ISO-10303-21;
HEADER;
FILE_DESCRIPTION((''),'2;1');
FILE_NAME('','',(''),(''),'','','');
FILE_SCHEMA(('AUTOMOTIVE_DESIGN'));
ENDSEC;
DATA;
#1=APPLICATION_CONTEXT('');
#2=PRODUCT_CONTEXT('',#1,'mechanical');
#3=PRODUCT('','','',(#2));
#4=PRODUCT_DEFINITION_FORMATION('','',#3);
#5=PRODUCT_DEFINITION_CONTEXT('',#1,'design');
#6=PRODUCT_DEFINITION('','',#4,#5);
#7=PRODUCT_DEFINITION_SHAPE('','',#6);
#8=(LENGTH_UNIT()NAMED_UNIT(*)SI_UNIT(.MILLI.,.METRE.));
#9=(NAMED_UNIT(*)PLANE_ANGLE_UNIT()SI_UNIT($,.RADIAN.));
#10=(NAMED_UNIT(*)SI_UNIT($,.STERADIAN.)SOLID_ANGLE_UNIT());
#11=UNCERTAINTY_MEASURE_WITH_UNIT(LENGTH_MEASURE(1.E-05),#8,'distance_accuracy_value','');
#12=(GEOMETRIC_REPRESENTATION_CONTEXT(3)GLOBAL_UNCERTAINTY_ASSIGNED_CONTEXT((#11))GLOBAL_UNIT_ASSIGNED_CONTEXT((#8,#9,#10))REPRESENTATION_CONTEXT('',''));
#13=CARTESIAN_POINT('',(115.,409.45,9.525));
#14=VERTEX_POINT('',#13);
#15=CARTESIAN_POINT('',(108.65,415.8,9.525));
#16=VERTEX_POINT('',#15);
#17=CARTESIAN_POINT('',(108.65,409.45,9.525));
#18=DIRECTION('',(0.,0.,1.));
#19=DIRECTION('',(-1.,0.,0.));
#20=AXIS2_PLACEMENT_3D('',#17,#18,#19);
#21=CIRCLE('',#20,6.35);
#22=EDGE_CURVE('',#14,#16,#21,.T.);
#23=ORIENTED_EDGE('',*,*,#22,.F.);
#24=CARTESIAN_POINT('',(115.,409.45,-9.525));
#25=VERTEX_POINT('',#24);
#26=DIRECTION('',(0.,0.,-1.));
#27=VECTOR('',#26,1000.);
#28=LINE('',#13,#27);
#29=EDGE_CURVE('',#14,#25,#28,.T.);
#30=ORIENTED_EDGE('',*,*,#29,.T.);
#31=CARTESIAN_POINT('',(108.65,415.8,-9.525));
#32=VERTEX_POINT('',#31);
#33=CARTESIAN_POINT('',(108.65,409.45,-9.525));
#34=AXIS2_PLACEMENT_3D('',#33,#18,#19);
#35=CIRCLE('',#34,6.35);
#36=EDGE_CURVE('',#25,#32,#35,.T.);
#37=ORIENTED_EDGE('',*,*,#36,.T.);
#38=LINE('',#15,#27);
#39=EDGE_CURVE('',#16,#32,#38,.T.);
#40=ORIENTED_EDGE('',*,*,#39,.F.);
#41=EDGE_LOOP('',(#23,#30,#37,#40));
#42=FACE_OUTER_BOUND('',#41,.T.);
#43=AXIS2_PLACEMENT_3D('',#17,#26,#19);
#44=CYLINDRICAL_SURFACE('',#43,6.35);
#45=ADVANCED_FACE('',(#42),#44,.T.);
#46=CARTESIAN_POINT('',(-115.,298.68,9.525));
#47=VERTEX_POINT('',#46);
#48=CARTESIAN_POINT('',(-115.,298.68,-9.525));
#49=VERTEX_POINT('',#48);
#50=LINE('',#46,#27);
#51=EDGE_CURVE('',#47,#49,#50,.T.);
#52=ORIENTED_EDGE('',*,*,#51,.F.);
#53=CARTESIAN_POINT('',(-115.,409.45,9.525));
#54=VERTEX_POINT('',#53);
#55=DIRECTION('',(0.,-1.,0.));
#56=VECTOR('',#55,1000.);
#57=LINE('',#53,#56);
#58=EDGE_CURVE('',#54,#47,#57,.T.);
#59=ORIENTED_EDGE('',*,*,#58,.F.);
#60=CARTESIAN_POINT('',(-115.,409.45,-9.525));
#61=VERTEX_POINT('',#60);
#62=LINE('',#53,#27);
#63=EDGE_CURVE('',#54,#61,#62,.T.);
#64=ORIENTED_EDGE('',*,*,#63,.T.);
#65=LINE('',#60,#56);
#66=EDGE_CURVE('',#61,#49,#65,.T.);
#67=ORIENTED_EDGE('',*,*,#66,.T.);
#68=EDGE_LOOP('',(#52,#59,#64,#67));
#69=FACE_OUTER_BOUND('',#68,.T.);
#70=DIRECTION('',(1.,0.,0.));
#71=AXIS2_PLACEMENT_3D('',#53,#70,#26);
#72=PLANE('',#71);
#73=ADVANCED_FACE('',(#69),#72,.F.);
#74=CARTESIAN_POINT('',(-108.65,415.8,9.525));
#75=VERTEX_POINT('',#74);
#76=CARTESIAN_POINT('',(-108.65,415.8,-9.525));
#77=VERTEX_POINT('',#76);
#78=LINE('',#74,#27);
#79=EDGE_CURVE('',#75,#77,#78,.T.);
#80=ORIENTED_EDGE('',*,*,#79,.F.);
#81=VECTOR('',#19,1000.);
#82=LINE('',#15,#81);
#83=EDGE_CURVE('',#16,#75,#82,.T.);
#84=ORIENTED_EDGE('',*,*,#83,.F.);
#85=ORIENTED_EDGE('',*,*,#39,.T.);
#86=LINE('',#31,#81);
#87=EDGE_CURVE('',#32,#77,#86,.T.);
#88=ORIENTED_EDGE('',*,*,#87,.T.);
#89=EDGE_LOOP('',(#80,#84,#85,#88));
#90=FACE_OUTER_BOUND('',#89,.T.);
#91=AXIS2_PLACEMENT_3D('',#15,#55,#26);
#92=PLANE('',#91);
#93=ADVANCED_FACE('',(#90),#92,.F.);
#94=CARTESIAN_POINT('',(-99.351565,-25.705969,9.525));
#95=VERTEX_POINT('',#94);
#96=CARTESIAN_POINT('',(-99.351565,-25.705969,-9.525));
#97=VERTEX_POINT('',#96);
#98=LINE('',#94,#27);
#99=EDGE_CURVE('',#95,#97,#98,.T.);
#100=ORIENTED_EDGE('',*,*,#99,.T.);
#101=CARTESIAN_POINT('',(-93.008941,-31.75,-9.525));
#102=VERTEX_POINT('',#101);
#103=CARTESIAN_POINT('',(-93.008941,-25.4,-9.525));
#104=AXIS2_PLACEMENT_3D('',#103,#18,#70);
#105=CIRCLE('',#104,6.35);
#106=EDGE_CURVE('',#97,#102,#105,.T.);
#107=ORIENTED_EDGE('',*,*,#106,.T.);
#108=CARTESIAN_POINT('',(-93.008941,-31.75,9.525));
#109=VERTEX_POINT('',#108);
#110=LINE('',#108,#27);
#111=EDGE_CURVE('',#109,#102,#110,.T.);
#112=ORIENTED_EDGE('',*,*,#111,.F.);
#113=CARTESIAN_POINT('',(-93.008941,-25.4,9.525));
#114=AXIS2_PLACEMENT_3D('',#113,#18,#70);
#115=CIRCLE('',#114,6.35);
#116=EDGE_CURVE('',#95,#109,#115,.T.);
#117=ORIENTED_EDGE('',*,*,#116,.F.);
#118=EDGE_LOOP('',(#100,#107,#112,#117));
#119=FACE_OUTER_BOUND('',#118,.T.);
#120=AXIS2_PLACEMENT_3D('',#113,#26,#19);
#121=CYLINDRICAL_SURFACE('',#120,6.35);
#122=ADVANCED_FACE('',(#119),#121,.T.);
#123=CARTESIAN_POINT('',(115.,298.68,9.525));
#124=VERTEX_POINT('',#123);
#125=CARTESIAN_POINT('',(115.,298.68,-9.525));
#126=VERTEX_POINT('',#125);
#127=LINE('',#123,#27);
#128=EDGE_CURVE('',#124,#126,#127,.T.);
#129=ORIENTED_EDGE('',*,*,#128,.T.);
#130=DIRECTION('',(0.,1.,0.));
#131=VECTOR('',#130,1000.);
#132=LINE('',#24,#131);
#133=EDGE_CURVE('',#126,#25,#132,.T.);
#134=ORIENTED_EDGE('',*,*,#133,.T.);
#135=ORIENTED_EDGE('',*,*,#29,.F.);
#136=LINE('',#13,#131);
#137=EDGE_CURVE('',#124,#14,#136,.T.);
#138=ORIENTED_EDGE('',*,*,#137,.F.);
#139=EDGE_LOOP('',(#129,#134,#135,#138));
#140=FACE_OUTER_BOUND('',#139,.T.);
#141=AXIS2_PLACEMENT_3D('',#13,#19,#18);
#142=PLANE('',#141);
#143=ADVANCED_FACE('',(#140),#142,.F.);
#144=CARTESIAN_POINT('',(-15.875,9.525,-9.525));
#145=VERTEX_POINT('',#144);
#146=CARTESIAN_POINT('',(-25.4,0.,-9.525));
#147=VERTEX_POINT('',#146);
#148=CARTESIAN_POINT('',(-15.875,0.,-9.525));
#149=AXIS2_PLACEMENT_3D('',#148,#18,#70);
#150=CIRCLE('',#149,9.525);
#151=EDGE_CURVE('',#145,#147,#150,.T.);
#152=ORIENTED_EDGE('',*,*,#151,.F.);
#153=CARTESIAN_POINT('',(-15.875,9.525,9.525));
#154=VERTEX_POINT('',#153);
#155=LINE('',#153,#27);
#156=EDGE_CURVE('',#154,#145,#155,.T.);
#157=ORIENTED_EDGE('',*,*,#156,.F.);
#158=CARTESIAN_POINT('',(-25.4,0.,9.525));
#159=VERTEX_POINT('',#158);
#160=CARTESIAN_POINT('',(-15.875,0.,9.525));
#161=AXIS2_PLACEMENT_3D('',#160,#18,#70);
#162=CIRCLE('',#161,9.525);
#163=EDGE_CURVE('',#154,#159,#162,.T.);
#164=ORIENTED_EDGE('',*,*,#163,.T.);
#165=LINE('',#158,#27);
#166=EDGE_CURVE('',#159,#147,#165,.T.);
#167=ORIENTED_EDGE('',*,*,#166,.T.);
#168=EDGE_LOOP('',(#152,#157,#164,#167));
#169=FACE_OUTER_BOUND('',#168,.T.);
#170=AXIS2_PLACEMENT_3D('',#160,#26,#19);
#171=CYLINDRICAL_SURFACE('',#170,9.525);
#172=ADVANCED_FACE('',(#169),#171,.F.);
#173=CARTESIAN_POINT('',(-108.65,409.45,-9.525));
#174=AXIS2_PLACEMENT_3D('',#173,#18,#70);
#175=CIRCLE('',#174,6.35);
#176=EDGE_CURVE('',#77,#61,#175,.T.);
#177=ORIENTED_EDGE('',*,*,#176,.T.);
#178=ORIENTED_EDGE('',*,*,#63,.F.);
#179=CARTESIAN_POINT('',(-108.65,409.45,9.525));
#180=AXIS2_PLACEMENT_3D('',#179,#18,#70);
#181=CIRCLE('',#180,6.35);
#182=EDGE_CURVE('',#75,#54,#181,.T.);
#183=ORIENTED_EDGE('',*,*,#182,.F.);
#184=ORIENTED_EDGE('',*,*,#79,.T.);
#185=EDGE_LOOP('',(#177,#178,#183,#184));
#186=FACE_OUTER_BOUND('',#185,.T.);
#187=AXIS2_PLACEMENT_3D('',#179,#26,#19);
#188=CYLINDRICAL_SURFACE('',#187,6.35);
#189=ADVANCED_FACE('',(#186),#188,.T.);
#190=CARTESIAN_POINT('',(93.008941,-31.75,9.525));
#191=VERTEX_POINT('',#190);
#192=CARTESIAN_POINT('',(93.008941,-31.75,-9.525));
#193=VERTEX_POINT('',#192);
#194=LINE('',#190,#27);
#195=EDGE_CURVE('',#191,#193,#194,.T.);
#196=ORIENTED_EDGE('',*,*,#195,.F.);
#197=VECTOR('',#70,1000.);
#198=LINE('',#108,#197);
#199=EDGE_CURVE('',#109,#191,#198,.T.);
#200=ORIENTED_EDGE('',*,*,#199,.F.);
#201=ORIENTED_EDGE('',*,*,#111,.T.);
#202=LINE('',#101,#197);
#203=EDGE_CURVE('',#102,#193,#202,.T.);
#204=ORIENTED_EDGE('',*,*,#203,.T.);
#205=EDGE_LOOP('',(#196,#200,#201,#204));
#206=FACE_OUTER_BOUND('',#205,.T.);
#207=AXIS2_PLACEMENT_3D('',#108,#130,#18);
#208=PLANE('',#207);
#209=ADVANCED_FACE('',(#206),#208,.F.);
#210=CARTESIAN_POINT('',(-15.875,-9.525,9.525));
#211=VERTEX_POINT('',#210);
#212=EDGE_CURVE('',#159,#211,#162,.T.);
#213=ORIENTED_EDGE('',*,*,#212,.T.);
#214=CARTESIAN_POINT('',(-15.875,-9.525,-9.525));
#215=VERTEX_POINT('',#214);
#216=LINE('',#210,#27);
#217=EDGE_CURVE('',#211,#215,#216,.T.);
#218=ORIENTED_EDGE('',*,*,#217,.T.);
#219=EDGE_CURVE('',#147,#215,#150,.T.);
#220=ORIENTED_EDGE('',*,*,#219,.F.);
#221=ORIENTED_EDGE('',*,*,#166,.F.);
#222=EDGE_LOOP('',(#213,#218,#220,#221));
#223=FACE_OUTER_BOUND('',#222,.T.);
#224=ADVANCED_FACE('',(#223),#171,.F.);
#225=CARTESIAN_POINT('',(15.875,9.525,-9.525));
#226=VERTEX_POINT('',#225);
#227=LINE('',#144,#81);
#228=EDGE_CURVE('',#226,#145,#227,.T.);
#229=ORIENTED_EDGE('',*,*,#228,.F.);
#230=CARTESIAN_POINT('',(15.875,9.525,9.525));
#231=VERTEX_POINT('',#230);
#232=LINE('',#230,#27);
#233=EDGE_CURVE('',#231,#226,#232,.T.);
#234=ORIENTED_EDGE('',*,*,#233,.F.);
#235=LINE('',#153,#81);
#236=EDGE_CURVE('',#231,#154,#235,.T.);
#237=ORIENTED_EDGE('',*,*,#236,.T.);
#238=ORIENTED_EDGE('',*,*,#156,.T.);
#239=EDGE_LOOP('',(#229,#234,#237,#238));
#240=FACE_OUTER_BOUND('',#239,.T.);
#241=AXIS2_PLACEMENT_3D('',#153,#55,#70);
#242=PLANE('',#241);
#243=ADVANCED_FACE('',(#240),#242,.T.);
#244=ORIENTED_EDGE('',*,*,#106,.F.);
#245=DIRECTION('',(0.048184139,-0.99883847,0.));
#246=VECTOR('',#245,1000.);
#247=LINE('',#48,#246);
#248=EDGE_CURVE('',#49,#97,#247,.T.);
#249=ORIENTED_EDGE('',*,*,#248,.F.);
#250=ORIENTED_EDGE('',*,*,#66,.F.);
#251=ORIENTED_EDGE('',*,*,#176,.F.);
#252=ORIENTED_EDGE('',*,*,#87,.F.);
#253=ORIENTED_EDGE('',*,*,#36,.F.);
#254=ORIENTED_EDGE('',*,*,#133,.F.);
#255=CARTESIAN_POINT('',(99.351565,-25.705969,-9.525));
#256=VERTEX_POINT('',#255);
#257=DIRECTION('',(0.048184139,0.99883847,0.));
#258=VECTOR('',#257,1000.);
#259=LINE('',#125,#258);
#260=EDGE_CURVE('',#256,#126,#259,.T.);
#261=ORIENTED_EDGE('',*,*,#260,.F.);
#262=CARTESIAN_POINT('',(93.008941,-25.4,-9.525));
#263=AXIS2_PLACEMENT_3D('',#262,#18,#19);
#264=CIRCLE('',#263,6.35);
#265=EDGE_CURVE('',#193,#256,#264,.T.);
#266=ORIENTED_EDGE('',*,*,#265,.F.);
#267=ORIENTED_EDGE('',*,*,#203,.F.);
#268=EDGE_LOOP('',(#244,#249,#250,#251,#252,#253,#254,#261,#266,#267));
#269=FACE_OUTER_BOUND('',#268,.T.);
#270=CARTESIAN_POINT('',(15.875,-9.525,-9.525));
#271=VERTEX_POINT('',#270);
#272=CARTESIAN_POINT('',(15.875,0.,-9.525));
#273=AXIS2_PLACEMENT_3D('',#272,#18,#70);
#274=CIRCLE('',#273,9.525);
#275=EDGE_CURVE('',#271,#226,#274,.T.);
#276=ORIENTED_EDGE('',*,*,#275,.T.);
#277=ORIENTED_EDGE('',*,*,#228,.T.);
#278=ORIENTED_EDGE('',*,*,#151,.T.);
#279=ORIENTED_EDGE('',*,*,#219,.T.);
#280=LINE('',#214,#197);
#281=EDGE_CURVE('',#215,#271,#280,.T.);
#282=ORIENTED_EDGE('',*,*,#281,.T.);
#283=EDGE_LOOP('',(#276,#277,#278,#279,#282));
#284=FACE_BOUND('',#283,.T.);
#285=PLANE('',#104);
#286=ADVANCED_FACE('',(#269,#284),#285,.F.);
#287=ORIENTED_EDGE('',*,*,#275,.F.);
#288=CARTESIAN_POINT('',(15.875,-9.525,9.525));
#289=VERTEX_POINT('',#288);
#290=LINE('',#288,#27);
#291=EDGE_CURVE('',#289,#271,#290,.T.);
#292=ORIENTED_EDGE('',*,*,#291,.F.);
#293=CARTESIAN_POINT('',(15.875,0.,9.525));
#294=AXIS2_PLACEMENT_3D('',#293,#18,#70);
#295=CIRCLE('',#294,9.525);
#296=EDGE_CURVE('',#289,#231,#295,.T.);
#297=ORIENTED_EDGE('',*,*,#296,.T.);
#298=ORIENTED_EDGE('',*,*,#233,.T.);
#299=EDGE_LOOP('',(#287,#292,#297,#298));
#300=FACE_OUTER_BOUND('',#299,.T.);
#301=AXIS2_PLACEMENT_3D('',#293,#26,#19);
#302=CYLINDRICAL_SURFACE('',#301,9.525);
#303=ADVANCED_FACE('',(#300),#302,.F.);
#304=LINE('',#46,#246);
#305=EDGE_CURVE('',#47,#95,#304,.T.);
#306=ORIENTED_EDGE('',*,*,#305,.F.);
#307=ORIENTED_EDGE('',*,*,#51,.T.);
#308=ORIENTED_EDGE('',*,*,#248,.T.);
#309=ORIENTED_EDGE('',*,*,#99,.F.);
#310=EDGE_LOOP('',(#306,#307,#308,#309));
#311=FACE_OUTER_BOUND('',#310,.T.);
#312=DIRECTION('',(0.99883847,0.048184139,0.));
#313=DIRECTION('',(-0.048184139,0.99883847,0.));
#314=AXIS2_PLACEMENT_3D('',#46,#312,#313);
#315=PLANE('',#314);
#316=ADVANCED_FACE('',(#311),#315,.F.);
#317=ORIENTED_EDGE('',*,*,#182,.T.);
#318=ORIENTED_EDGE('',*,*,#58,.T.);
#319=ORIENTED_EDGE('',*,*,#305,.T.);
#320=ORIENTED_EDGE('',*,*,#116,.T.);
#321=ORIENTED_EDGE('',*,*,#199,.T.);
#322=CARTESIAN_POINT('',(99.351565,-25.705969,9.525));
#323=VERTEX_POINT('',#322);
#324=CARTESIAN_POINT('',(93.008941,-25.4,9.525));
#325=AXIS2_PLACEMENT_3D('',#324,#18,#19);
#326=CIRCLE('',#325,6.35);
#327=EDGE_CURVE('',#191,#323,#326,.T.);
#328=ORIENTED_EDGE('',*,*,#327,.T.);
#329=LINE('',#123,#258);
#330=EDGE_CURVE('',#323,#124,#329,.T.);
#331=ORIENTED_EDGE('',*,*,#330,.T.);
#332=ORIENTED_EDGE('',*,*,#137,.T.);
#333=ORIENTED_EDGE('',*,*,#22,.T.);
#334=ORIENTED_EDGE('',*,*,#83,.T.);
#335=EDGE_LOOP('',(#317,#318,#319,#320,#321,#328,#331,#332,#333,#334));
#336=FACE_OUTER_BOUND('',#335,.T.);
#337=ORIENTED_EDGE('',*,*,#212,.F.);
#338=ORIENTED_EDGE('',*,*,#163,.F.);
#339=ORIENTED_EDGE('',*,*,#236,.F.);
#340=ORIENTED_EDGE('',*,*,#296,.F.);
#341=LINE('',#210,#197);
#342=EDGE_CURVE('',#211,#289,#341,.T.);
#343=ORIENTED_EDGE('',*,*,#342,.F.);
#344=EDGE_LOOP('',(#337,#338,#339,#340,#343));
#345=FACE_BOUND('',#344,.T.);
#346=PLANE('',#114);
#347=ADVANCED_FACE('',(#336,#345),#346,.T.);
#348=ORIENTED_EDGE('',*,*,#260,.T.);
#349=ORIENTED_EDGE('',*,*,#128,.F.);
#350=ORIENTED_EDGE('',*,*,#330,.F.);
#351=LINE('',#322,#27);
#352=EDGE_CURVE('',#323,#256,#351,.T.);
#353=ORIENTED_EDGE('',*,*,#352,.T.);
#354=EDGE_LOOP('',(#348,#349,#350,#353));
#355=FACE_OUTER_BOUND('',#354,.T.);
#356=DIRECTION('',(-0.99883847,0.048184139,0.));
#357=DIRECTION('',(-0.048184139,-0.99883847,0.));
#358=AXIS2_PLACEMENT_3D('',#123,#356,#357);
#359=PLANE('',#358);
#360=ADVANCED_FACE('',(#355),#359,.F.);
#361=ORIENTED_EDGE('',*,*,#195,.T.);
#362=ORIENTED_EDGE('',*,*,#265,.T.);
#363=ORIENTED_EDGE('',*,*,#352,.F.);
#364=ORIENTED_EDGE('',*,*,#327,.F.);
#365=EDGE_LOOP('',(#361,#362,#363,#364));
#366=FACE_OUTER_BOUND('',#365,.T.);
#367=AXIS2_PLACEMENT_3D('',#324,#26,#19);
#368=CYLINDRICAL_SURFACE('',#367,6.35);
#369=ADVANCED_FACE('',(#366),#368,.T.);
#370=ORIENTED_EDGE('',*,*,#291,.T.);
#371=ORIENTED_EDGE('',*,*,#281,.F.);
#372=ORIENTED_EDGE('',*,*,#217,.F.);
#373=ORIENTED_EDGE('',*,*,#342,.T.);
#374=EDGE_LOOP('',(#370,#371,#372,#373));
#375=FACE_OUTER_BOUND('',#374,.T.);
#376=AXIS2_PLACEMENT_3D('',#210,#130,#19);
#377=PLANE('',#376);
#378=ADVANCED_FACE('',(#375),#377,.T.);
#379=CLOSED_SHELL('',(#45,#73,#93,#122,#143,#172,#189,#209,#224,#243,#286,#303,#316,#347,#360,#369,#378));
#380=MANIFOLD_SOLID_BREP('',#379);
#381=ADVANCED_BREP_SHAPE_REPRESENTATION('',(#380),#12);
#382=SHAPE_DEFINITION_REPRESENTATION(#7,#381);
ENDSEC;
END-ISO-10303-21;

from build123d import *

# Parameters (mm, degrees)
BOSS_EXTRUDE1_DEPTH = 9.525


with BuildPart() as part:
    # Sketch1 → Boss-Extrude1 (new, symmetric)
    with BuildSketch(Plane.XY):
        with BuildLine():
            Line((108.65, 415.8), (-108.65, 415.8))
            ThreePointArc((-108.65, 415.8), (-113.140128061, 413.940128061), (-115, 409.45))
            Line((-115, 409.45), (-115, 298.68))
            Line((-115, 298.68), (-99.351565081, -25.705969286))
            ThreePointArc((-99.351565081, -25.705969286), (-97.389556909, -29.997031921), (-93.008940798, -31.75))
            Line((-93.008940798, -31.75), (93.008940798, -31.75))
            ThreePointArc((93.008940798, -31.75), (97.389556909, -29.997031921), (99.351565081, -25.705969286))
            Line((99.351565081, -25.705969286), (115, 298.68))
            Line((115, 298.68), (115, 409.45))
            ThreePointArc((115, 409.45), (113.140128061, 413.940128061), (108.65, 415.8))
        make_face()
        with BuildLine():
            Line((-15.875, 9.525), (15.875, 9.525))
            ThreePointArc((15.875, 9.525), (25.4, 0), (15.875, -9.525))
            Line((15.875, -9.525), (-15.875, -9.525))
            ThreePointArc((-15.875, -9.525), (-25.4, 0), (-15.875, 9.525))
        make_face(mode=Mode.SUBTRACT)
    extrude(amount=BOSS_EXTRUDE1_DEPTH, both=True)


solid = part.part
